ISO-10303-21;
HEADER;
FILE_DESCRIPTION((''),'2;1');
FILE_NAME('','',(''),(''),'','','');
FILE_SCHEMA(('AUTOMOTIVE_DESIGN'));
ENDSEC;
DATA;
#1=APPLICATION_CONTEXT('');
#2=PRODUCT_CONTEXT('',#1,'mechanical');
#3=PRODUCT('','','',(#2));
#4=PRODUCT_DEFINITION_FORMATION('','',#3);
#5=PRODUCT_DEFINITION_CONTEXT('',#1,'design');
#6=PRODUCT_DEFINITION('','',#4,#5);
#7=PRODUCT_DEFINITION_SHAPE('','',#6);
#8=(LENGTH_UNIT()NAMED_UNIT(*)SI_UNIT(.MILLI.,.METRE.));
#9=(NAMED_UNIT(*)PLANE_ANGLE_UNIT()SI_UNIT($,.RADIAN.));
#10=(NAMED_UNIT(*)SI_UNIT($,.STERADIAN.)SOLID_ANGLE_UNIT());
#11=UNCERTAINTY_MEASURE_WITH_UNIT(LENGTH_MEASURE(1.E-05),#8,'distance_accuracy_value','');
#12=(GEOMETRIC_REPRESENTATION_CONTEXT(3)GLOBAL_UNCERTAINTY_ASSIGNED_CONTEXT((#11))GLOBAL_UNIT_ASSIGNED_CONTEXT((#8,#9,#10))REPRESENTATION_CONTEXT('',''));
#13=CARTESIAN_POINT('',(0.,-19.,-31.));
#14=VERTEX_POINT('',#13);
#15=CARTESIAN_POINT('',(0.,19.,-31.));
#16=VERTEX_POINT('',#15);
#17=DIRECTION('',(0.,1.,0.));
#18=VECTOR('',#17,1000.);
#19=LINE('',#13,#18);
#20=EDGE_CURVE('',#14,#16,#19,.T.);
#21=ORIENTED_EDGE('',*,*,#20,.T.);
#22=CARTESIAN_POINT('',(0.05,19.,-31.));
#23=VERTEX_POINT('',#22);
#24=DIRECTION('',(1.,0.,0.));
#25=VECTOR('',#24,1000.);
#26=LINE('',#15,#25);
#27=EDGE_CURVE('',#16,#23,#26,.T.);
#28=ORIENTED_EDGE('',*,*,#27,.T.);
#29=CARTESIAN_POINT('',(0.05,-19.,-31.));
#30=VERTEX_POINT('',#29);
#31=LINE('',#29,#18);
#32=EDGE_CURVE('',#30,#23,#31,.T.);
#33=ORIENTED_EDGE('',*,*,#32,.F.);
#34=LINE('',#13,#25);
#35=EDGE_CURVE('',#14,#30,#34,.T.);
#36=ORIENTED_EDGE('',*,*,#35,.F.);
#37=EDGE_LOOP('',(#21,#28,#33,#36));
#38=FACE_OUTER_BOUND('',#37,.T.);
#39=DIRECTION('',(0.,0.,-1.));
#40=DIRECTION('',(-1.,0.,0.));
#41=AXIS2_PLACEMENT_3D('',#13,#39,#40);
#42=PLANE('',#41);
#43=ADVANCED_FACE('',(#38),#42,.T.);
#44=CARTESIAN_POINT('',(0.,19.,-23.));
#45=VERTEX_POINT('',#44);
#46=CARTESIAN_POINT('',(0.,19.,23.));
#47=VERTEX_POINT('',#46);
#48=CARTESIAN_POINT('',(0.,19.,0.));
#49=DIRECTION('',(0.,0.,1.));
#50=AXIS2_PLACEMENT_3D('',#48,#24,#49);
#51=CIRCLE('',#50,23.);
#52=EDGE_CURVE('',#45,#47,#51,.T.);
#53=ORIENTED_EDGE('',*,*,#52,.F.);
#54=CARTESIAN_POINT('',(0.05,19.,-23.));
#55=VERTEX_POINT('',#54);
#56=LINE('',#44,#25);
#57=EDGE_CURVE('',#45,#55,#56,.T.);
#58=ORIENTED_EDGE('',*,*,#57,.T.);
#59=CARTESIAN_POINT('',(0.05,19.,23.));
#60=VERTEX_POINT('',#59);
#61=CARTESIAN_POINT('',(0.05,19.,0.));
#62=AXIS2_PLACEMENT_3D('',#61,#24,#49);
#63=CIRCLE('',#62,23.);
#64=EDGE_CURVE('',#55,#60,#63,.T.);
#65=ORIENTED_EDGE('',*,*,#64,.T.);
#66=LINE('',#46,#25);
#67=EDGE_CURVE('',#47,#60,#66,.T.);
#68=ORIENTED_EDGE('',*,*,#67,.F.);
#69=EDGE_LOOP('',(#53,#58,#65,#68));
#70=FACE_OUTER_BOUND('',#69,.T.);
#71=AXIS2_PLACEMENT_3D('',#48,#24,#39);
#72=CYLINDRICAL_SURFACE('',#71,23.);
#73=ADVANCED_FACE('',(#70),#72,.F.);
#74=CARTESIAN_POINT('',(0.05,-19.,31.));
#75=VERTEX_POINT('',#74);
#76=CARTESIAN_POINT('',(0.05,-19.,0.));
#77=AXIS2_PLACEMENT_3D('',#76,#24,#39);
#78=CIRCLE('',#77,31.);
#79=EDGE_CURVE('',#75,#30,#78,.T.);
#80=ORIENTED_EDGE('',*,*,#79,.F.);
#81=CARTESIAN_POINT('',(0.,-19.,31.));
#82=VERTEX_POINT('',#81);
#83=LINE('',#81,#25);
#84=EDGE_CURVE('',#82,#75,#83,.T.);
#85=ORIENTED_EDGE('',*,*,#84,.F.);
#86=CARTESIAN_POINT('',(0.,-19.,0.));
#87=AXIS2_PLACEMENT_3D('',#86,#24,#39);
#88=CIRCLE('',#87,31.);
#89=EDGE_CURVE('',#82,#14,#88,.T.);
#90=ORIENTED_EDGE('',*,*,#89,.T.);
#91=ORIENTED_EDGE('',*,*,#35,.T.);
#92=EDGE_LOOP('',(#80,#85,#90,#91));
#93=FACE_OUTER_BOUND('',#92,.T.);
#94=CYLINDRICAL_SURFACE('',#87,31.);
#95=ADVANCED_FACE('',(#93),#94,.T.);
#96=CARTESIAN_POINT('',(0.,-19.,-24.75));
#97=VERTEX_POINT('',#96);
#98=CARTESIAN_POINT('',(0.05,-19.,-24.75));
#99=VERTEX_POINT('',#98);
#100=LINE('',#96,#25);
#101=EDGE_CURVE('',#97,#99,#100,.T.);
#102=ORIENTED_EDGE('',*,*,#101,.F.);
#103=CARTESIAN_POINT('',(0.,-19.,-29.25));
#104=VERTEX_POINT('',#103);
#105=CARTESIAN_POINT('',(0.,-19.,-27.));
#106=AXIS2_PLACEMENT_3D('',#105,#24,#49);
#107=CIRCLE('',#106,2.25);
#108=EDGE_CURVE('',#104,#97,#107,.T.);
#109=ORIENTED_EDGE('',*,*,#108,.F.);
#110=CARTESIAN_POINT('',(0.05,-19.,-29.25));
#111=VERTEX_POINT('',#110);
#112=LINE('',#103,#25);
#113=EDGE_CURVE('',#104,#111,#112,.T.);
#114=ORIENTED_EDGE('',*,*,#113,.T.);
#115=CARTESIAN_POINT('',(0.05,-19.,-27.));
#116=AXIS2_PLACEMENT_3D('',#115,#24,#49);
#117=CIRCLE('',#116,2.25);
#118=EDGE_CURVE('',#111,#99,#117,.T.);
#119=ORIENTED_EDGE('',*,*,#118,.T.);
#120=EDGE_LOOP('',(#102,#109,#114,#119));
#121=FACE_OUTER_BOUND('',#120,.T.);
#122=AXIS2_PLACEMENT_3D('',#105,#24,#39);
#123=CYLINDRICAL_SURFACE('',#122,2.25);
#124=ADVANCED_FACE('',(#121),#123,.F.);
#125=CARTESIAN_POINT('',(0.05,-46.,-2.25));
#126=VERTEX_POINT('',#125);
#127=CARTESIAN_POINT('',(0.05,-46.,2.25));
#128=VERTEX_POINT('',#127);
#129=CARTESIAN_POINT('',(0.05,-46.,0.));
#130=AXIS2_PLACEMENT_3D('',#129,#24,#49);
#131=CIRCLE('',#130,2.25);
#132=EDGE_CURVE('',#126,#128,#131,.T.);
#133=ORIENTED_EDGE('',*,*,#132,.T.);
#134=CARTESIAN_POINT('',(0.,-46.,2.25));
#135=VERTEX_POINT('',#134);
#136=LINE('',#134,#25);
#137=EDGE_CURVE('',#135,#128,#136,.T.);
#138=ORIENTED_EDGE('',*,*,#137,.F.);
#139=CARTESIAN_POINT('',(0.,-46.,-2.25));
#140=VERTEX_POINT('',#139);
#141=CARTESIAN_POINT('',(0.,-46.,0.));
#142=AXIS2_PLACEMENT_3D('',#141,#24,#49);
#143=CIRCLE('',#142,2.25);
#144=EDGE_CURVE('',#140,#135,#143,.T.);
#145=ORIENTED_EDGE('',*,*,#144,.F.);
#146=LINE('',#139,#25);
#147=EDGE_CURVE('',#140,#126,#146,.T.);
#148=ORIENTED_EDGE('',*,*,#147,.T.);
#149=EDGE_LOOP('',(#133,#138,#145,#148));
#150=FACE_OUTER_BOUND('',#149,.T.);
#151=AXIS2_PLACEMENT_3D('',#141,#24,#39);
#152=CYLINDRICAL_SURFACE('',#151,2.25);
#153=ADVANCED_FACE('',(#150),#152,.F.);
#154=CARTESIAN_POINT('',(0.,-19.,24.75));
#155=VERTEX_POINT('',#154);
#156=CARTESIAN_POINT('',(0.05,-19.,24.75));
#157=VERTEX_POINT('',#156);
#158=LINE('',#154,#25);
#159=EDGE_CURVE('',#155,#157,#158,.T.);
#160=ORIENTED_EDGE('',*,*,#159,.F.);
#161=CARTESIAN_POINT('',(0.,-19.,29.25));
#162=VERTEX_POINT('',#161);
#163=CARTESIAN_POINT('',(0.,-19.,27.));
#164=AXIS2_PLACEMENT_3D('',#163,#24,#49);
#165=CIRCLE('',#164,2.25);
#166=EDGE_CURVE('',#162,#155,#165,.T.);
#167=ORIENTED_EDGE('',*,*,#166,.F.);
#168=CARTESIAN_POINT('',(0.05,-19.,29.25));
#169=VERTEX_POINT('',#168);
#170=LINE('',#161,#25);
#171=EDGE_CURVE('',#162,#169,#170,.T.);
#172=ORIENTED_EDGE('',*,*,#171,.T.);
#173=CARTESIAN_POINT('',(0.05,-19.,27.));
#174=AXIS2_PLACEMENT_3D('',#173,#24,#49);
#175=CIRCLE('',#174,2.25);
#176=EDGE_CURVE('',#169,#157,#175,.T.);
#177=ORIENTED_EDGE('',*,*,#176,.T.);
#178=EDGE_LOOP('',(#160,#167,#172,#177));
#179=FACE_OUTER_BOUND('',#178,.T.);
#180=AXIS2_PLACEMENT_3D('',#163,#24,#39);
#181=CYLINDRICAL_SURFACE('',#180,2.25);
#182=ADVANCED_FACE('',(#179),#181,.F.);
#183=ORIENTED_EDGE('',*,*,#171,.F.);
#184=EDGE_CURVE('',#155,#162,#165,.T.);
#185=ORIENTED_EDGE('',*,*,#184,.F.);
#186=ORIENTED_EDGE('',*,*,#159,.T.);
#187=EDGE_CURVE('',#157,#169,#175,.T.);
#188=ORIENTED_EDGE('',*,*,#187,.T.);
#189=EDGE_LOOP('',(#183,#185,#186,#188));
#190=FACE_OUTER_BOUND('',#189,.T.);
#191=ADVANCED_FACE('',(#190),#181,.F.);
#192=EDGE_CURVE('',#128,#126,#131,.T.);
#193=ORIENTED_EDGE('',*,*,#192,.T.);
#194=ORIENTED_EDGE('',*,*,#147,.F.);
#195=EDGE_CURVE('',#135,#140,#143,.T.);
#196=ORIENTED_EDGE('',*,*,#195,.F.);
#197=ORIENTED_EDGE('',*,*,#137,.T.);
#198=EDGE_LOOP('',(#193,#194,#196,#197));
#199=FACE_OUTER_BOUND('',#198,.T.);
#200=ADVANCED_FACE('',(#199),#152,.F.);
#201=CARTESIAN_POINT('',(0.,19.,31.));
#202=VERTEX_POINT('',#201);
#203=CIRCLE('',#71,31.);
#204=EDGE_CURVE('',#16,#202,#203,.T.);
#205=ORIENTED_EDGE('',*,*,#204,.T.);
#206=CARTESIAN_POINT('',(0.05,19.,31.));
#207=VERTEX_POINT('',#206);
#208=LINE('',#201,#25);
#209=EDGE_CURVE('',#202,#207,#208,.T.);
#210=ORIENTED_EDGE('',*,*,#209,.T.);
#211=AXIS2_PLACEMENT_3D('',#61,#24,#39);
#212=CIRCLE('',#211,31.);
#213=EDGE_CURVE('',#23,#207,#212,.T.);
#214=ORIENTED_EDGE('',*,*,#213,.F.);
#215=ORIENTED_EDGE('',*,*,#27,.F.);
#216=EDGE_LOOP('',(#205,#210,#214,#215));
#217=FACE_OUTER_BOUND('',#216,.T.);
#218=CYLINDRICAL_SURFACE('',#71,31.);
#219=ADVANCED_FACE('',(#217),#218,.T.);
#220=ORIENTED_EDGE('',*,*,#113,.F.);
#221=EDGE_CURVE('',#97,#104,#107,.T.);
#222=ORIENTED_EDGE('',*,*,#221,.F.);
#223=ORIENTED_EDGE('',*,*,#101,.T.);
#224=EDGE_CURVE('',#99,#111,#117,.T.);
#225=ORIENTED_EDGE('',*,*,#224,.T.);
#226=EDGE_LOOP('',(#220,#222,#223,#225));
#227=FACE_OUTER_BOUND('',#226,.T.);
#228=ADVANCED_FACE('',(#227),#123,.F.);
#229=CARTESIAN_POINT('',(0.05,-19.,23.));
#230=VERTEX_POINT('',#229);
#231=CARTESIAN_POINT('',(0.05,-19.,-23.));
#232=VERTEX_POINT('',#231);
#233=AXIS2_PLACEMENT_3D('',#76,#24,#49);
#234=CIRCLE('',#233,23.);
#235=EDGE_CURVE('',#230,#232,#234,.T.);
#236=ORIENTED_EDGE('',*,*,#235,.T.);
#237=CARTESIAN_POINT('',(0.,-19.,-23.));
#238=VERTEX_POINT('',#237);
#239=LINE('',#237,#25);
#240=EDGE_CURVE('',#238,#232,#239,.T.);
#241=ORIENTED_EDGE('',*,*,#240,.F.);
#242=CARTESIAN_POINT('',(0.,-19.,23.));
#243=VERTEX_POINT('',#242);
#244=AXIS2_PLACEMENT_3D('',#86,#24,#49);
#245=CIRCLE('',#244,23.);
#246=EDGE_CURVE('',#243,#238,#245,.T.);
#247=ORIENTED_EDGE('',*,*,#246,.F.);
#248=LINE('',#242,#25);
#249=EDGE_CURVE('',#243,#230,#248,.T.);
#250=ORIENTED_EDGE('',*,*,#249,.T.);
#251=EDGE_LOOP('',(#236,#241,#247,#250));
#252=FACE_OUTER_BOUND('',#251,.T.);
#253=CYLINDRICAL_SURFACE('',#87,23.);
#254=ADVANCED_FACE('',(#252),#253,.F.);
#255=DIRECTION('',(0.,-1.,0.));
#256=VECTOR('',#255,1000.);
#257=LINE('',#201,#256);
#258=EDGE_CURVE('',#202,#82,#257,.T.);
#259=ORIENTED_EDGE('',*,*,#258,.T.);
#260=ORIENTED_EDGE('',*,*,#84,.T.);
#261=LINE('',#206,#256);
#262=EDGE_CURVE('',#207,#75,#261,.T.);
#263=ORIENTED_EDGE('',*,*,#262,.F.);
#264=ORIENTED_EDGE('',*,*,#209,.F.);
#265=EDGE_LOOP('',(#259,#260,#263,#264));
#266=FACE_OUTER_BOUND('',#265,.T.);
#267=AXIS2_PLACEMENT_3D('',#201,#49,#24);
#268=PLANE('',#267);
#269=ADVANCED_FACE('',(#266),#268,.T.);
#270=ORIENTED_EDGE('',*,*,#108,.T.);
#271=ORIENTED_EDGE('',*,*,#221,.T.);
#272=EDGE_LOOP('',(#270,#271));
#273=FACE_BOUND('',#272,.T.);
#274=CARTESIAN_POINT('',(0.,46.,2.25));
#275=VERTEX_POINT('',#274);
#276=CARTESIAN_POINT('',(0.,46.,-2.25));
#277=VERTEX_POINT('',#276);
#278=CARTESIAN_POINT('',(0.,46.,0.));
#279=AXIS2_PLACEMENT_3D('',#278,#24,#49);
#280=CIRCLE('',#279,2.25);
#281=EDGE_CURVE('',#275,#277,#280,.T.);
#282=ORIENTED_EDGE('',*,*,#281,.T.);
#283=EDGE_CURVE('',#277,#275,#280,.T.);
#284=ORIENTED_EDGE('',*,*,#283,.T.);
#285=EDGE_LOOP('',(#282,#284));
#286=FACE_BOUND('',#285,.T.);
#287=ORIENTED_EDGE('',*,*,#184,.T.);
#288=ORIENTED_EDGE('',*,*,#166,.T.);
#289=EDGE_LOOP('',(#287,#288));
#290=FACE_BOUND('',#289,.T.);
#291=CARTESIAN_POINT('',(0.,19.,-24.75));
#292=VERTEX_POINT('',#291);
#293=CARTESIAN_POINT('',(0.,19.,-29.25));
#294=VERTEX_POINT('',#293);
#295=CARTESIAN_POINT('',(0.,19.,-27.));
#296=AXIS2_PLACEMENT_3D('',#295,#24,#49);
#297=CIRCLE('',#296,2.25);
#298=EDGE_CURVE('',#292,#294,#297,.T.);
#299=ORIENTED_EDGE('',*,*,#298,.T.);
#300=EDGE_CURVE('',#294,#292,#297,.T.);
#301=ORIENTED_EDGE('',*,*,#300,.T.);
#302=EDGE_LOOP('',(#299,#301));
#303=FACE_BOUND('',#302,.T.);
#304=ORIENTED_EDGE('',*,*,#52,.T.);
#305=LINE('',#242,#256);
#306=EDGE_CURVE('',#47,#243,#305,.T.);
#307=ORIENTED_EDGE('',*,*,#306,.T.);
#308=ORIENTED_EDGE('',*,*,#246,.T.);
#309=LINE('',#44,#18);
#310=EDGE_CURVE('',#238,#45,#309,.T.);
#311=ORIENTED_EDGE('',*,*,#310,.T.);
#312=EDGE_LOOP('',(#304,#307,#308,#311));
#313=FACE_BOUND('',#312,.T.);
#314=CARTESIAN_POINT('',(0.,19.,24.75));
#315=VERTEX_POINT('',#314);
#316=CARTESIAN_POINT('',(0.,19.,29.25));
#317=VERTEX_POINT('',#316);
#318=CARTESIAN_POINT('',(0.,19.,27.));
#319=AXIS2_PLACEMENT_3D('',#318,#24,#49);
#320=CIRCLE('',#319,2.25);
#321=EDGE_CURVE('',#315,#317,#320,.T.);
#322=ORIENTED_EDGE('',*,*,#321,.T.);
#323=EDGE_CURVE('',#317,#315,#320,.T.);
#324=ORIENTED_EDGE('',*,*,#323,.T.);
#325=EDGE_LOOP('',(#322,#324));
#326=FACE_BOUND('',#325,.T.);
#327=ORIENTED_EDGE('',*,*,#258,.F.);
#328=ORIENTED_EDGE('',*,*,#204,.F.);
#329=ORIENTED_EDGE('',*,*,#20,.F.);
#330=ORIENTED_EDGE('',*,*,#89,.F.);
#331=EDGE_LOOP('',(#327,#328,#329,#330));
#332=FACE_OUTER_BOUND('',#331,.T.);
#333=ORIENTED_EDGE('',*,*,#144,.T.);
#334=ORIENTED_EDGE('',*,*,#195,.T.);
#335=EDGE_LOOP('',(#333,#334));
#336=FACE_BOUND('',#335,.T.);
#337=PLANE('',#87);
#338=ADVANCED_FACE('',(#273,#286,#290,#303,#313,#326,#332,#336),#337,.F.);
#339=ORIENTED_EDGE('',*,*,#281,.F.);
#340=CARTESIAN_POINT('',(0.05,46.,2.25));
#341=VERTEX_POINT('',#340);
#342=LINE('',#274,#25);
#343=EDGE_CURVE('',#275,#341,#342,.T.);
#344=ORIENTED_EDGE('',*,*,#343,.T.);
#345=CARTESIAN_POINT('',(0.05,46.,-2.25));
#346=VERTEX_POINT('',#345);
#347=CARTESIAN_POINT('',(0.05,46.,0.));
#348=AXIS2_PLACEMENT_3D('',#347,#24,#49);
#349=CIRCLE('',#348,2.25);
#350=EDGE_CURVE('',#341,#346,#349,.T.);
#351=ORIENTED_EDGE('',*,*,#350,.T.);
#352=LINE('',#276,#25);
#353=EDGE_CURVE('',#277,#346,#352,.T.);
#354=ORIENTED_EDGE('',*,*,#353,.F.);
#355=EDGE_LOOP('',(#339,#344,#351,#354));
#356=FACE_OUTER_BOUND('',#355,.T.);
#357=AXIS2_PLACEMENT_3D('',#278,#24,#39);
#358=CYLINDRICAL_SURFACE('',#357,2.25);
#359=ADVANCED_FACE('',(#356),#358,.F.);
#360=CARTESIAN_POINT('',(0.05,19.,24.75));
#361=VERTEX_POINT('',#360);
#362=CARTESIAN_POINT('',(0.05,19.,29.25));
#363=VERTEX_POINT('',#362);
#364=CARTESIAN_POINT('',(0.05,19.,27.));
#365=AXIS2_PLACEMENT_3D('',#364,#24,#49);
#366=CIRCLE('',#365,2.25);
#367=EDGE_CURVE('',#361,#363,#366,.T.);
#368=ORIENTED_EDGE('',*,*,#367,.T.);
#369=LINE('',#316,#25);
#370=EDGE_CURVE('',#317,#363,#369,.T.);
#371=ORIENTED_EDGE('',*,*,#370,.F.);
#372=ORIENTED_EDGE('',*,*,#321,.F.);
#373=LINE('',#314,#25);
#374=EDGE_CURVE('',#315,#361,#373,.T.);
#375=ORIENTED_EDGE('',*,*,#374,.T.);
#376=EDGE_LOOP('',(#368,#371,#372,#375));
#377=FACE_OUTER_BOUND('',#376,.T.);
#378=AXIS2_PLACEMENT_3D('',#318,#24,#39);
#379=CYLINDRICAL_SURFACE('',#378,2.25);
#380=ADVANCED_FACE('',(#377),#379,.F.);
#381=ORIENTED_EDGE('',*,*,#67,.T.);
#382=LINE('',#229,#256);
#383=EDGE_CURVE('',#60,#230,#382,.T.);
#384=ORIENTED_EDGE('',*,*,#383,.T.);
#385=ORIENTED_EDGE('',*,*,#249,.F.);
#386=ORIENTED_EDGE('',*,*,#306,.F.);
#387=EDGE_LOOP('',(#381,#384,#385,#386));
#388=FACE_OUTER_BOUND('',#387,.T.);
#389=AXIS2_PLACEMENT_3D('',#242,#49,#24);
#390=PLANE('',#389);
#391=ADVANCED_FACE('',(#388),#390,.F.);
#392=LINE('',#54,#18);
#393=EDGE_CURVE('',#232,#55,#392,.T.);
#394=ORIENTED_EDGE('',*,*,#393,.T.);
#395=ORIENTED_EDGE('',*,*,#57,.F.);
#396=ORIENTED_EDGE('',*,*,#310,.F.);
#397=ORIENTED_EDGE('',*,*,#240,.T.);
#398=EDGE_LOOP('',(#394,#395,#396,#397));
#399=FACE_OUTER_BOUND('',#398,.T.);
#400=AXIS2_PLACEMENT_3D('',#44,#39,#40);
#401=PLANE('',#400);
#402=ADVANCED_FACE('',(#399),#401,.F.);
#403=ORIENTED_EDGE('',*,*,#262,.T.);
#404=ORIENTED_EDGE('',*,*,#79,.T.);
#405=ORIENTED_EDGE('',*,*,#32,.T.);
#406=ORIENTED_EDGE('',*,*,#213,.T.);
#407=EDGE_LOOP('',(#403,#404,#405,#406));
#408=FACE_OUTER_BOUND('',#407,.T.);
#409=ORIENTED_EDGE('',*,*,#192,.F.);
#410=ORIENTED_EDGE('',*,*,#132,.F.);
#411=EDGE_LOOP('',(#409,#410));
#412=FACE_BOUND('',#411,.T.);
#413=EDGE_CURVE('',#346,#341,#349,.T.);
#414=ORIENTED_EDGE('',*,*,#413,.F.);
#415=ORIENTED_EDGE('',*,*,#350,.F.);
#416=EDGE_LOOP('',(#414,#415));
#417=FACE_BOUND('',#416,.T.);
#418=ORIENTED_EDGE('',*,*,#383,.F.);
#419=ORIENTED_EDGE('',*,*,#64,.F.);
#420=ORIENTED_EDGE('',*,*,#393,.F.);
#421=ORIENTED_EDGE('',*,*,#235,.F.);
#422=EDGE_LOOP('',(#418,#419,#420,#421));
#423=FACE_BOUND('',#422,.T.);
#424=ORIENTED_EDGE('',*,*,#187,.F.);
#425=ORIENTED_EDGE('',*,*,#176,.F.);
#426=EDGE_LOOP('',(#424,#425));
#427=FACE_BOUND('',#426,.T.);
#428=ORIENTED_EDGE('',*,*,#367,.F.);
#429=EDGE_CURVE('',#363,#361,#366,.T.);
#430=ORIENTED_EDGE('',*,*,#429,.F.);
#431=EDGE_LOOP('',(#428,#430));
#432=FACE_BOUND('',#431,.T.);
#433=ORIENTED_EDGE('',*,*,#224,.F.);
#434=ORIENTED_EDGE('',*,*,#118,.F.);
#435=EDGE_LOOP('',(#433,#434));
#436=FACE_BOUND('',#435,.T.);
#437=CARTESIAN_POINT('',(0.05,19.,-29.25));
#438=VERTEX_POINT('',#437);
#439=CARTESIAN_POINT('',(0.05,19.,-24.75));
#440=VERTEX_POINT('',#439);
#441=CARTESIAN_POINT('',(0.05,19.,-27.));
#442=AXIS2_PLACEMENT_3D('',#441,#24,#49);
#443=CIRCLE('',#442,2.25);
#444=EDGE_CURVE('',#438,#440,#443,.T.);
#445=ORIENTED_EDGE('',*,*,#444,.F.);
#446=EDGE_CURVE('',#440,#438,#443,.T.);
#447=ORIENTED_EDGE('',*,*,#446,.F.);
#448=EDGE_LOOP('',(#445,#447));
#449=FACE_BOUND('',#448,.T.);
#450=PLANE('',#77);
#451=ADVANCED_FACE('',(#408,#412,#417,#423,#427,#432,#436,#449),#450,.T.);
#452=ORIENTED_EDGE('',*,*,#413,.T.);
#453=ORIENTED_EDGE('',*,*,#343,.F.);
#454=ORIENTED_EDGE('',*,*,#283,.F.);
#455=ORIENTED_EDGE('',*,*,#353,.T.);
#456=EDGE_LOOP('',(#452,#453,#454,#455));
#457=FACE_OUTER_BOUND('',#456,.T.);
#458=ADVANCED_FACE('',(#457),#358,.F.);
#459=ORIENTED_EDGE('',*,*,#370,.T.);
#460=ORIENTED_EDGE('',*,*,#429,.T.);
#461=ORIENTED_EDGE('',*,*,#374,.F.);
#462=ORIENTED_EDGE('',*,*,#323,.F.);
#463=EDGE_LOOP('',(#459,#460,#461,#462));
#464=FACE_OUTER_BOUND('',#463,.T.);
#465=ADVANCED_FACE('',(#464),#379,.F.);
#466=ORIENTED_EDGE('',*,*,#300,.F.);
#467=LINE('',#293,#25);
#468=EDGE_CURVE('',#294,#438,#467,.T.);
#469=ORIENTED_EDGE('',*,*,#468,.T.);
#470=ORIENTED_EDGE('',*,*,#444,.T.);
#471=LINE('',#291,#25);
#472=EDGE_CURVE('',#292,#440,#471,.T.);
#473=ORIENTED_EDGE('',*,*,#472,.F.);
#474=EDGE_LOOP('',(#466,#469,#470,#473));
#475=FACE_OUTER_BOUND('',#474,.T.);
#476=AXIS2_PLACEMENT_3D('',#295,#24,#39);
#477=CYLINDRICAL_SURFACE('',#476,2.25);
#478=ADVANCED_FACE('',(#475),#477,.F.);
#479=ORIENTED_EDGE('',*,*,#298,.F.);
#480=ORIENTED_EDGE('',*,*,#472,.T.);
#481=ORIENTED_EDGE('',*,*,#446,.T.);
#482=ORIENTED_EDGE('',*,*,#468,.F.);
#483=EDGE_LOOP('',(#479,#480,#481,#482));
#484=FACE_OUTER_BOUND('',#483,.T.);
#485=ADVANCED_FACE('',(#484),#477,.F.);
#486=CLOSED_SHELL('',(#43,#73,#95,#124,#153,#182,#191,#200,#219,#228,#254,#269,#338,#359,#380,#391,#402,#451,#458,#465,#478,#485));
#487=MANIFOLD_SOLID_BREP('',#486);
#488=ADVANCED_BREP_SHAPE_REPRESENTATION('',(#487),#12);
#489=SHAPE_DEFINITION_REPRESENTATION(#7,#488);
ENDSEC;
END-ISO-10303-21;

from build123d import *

# Parameters (mm, degrees)
SKETCH1_R           = 2.25
BOSS_EXTRUDE1_DEPTH = 0.05


with BuildPart() as part:
    # Sketch1 → Boss-Extrude1 (new body)
    with BuildSketch(Plane(origin=(0.05, 0, 0), x_dir=(0, 0, -1), z_dir=(1, 0, 0))):
        with BuildLine():
            Line((31, -19), (31, 19))
            ThreePointArc((31, 19), (0, 50), (-31, 19))
            Line((-31, 19), (-31, -19))
            ThreePointArc((-31, -19), (0, -50), (31, -19))
        make_face()
        with Locations(Location((27, -19, 0), (0, 0, 180))):
            Circle(SKETCH1_R, mode=Mode.SUBTRACT)
        with Locations(Location((27, 19, 0), (0, 0, 180))):
            Circle(SKETCH1_R, mode=Mode.SUBTRACT)
        with Locations(Location((0, 46, 0), (0, 0, 180))):
            Circle(SKETCH1_R, mode=Mode.SUBTRACT)
        with Locations(Location((-27, 19, 0), (0, 0, 180))):
            Circle(SKETCH1_R, mode=Mode.SUBTRACT)
        with Locations(Location((-27, -19, 0), (0, 0, 180))):
            Circle(SKETCH1_R, mode=Mode.SUBTRACT)
        with Locations(Location((0, -46, 0), (0, 0, 180))):
            Circle(SKETCH1_R, mode=Mode.SUBTRACT)
        with BuildLine():
            Line((23, 19), (23, -19))
            ThreePointArc((23, -19), (0, -42), (-23, -19))
            Line((-23, -19), (-23, 19))
            ThreePointArc((-23, 19), (0, 42), (23, 19))
        make_face(mode=Mode.SUBTRACT)
    extrude(amount=-BOSS_EXTRUDE1_DEPTH)


solid = part.part
